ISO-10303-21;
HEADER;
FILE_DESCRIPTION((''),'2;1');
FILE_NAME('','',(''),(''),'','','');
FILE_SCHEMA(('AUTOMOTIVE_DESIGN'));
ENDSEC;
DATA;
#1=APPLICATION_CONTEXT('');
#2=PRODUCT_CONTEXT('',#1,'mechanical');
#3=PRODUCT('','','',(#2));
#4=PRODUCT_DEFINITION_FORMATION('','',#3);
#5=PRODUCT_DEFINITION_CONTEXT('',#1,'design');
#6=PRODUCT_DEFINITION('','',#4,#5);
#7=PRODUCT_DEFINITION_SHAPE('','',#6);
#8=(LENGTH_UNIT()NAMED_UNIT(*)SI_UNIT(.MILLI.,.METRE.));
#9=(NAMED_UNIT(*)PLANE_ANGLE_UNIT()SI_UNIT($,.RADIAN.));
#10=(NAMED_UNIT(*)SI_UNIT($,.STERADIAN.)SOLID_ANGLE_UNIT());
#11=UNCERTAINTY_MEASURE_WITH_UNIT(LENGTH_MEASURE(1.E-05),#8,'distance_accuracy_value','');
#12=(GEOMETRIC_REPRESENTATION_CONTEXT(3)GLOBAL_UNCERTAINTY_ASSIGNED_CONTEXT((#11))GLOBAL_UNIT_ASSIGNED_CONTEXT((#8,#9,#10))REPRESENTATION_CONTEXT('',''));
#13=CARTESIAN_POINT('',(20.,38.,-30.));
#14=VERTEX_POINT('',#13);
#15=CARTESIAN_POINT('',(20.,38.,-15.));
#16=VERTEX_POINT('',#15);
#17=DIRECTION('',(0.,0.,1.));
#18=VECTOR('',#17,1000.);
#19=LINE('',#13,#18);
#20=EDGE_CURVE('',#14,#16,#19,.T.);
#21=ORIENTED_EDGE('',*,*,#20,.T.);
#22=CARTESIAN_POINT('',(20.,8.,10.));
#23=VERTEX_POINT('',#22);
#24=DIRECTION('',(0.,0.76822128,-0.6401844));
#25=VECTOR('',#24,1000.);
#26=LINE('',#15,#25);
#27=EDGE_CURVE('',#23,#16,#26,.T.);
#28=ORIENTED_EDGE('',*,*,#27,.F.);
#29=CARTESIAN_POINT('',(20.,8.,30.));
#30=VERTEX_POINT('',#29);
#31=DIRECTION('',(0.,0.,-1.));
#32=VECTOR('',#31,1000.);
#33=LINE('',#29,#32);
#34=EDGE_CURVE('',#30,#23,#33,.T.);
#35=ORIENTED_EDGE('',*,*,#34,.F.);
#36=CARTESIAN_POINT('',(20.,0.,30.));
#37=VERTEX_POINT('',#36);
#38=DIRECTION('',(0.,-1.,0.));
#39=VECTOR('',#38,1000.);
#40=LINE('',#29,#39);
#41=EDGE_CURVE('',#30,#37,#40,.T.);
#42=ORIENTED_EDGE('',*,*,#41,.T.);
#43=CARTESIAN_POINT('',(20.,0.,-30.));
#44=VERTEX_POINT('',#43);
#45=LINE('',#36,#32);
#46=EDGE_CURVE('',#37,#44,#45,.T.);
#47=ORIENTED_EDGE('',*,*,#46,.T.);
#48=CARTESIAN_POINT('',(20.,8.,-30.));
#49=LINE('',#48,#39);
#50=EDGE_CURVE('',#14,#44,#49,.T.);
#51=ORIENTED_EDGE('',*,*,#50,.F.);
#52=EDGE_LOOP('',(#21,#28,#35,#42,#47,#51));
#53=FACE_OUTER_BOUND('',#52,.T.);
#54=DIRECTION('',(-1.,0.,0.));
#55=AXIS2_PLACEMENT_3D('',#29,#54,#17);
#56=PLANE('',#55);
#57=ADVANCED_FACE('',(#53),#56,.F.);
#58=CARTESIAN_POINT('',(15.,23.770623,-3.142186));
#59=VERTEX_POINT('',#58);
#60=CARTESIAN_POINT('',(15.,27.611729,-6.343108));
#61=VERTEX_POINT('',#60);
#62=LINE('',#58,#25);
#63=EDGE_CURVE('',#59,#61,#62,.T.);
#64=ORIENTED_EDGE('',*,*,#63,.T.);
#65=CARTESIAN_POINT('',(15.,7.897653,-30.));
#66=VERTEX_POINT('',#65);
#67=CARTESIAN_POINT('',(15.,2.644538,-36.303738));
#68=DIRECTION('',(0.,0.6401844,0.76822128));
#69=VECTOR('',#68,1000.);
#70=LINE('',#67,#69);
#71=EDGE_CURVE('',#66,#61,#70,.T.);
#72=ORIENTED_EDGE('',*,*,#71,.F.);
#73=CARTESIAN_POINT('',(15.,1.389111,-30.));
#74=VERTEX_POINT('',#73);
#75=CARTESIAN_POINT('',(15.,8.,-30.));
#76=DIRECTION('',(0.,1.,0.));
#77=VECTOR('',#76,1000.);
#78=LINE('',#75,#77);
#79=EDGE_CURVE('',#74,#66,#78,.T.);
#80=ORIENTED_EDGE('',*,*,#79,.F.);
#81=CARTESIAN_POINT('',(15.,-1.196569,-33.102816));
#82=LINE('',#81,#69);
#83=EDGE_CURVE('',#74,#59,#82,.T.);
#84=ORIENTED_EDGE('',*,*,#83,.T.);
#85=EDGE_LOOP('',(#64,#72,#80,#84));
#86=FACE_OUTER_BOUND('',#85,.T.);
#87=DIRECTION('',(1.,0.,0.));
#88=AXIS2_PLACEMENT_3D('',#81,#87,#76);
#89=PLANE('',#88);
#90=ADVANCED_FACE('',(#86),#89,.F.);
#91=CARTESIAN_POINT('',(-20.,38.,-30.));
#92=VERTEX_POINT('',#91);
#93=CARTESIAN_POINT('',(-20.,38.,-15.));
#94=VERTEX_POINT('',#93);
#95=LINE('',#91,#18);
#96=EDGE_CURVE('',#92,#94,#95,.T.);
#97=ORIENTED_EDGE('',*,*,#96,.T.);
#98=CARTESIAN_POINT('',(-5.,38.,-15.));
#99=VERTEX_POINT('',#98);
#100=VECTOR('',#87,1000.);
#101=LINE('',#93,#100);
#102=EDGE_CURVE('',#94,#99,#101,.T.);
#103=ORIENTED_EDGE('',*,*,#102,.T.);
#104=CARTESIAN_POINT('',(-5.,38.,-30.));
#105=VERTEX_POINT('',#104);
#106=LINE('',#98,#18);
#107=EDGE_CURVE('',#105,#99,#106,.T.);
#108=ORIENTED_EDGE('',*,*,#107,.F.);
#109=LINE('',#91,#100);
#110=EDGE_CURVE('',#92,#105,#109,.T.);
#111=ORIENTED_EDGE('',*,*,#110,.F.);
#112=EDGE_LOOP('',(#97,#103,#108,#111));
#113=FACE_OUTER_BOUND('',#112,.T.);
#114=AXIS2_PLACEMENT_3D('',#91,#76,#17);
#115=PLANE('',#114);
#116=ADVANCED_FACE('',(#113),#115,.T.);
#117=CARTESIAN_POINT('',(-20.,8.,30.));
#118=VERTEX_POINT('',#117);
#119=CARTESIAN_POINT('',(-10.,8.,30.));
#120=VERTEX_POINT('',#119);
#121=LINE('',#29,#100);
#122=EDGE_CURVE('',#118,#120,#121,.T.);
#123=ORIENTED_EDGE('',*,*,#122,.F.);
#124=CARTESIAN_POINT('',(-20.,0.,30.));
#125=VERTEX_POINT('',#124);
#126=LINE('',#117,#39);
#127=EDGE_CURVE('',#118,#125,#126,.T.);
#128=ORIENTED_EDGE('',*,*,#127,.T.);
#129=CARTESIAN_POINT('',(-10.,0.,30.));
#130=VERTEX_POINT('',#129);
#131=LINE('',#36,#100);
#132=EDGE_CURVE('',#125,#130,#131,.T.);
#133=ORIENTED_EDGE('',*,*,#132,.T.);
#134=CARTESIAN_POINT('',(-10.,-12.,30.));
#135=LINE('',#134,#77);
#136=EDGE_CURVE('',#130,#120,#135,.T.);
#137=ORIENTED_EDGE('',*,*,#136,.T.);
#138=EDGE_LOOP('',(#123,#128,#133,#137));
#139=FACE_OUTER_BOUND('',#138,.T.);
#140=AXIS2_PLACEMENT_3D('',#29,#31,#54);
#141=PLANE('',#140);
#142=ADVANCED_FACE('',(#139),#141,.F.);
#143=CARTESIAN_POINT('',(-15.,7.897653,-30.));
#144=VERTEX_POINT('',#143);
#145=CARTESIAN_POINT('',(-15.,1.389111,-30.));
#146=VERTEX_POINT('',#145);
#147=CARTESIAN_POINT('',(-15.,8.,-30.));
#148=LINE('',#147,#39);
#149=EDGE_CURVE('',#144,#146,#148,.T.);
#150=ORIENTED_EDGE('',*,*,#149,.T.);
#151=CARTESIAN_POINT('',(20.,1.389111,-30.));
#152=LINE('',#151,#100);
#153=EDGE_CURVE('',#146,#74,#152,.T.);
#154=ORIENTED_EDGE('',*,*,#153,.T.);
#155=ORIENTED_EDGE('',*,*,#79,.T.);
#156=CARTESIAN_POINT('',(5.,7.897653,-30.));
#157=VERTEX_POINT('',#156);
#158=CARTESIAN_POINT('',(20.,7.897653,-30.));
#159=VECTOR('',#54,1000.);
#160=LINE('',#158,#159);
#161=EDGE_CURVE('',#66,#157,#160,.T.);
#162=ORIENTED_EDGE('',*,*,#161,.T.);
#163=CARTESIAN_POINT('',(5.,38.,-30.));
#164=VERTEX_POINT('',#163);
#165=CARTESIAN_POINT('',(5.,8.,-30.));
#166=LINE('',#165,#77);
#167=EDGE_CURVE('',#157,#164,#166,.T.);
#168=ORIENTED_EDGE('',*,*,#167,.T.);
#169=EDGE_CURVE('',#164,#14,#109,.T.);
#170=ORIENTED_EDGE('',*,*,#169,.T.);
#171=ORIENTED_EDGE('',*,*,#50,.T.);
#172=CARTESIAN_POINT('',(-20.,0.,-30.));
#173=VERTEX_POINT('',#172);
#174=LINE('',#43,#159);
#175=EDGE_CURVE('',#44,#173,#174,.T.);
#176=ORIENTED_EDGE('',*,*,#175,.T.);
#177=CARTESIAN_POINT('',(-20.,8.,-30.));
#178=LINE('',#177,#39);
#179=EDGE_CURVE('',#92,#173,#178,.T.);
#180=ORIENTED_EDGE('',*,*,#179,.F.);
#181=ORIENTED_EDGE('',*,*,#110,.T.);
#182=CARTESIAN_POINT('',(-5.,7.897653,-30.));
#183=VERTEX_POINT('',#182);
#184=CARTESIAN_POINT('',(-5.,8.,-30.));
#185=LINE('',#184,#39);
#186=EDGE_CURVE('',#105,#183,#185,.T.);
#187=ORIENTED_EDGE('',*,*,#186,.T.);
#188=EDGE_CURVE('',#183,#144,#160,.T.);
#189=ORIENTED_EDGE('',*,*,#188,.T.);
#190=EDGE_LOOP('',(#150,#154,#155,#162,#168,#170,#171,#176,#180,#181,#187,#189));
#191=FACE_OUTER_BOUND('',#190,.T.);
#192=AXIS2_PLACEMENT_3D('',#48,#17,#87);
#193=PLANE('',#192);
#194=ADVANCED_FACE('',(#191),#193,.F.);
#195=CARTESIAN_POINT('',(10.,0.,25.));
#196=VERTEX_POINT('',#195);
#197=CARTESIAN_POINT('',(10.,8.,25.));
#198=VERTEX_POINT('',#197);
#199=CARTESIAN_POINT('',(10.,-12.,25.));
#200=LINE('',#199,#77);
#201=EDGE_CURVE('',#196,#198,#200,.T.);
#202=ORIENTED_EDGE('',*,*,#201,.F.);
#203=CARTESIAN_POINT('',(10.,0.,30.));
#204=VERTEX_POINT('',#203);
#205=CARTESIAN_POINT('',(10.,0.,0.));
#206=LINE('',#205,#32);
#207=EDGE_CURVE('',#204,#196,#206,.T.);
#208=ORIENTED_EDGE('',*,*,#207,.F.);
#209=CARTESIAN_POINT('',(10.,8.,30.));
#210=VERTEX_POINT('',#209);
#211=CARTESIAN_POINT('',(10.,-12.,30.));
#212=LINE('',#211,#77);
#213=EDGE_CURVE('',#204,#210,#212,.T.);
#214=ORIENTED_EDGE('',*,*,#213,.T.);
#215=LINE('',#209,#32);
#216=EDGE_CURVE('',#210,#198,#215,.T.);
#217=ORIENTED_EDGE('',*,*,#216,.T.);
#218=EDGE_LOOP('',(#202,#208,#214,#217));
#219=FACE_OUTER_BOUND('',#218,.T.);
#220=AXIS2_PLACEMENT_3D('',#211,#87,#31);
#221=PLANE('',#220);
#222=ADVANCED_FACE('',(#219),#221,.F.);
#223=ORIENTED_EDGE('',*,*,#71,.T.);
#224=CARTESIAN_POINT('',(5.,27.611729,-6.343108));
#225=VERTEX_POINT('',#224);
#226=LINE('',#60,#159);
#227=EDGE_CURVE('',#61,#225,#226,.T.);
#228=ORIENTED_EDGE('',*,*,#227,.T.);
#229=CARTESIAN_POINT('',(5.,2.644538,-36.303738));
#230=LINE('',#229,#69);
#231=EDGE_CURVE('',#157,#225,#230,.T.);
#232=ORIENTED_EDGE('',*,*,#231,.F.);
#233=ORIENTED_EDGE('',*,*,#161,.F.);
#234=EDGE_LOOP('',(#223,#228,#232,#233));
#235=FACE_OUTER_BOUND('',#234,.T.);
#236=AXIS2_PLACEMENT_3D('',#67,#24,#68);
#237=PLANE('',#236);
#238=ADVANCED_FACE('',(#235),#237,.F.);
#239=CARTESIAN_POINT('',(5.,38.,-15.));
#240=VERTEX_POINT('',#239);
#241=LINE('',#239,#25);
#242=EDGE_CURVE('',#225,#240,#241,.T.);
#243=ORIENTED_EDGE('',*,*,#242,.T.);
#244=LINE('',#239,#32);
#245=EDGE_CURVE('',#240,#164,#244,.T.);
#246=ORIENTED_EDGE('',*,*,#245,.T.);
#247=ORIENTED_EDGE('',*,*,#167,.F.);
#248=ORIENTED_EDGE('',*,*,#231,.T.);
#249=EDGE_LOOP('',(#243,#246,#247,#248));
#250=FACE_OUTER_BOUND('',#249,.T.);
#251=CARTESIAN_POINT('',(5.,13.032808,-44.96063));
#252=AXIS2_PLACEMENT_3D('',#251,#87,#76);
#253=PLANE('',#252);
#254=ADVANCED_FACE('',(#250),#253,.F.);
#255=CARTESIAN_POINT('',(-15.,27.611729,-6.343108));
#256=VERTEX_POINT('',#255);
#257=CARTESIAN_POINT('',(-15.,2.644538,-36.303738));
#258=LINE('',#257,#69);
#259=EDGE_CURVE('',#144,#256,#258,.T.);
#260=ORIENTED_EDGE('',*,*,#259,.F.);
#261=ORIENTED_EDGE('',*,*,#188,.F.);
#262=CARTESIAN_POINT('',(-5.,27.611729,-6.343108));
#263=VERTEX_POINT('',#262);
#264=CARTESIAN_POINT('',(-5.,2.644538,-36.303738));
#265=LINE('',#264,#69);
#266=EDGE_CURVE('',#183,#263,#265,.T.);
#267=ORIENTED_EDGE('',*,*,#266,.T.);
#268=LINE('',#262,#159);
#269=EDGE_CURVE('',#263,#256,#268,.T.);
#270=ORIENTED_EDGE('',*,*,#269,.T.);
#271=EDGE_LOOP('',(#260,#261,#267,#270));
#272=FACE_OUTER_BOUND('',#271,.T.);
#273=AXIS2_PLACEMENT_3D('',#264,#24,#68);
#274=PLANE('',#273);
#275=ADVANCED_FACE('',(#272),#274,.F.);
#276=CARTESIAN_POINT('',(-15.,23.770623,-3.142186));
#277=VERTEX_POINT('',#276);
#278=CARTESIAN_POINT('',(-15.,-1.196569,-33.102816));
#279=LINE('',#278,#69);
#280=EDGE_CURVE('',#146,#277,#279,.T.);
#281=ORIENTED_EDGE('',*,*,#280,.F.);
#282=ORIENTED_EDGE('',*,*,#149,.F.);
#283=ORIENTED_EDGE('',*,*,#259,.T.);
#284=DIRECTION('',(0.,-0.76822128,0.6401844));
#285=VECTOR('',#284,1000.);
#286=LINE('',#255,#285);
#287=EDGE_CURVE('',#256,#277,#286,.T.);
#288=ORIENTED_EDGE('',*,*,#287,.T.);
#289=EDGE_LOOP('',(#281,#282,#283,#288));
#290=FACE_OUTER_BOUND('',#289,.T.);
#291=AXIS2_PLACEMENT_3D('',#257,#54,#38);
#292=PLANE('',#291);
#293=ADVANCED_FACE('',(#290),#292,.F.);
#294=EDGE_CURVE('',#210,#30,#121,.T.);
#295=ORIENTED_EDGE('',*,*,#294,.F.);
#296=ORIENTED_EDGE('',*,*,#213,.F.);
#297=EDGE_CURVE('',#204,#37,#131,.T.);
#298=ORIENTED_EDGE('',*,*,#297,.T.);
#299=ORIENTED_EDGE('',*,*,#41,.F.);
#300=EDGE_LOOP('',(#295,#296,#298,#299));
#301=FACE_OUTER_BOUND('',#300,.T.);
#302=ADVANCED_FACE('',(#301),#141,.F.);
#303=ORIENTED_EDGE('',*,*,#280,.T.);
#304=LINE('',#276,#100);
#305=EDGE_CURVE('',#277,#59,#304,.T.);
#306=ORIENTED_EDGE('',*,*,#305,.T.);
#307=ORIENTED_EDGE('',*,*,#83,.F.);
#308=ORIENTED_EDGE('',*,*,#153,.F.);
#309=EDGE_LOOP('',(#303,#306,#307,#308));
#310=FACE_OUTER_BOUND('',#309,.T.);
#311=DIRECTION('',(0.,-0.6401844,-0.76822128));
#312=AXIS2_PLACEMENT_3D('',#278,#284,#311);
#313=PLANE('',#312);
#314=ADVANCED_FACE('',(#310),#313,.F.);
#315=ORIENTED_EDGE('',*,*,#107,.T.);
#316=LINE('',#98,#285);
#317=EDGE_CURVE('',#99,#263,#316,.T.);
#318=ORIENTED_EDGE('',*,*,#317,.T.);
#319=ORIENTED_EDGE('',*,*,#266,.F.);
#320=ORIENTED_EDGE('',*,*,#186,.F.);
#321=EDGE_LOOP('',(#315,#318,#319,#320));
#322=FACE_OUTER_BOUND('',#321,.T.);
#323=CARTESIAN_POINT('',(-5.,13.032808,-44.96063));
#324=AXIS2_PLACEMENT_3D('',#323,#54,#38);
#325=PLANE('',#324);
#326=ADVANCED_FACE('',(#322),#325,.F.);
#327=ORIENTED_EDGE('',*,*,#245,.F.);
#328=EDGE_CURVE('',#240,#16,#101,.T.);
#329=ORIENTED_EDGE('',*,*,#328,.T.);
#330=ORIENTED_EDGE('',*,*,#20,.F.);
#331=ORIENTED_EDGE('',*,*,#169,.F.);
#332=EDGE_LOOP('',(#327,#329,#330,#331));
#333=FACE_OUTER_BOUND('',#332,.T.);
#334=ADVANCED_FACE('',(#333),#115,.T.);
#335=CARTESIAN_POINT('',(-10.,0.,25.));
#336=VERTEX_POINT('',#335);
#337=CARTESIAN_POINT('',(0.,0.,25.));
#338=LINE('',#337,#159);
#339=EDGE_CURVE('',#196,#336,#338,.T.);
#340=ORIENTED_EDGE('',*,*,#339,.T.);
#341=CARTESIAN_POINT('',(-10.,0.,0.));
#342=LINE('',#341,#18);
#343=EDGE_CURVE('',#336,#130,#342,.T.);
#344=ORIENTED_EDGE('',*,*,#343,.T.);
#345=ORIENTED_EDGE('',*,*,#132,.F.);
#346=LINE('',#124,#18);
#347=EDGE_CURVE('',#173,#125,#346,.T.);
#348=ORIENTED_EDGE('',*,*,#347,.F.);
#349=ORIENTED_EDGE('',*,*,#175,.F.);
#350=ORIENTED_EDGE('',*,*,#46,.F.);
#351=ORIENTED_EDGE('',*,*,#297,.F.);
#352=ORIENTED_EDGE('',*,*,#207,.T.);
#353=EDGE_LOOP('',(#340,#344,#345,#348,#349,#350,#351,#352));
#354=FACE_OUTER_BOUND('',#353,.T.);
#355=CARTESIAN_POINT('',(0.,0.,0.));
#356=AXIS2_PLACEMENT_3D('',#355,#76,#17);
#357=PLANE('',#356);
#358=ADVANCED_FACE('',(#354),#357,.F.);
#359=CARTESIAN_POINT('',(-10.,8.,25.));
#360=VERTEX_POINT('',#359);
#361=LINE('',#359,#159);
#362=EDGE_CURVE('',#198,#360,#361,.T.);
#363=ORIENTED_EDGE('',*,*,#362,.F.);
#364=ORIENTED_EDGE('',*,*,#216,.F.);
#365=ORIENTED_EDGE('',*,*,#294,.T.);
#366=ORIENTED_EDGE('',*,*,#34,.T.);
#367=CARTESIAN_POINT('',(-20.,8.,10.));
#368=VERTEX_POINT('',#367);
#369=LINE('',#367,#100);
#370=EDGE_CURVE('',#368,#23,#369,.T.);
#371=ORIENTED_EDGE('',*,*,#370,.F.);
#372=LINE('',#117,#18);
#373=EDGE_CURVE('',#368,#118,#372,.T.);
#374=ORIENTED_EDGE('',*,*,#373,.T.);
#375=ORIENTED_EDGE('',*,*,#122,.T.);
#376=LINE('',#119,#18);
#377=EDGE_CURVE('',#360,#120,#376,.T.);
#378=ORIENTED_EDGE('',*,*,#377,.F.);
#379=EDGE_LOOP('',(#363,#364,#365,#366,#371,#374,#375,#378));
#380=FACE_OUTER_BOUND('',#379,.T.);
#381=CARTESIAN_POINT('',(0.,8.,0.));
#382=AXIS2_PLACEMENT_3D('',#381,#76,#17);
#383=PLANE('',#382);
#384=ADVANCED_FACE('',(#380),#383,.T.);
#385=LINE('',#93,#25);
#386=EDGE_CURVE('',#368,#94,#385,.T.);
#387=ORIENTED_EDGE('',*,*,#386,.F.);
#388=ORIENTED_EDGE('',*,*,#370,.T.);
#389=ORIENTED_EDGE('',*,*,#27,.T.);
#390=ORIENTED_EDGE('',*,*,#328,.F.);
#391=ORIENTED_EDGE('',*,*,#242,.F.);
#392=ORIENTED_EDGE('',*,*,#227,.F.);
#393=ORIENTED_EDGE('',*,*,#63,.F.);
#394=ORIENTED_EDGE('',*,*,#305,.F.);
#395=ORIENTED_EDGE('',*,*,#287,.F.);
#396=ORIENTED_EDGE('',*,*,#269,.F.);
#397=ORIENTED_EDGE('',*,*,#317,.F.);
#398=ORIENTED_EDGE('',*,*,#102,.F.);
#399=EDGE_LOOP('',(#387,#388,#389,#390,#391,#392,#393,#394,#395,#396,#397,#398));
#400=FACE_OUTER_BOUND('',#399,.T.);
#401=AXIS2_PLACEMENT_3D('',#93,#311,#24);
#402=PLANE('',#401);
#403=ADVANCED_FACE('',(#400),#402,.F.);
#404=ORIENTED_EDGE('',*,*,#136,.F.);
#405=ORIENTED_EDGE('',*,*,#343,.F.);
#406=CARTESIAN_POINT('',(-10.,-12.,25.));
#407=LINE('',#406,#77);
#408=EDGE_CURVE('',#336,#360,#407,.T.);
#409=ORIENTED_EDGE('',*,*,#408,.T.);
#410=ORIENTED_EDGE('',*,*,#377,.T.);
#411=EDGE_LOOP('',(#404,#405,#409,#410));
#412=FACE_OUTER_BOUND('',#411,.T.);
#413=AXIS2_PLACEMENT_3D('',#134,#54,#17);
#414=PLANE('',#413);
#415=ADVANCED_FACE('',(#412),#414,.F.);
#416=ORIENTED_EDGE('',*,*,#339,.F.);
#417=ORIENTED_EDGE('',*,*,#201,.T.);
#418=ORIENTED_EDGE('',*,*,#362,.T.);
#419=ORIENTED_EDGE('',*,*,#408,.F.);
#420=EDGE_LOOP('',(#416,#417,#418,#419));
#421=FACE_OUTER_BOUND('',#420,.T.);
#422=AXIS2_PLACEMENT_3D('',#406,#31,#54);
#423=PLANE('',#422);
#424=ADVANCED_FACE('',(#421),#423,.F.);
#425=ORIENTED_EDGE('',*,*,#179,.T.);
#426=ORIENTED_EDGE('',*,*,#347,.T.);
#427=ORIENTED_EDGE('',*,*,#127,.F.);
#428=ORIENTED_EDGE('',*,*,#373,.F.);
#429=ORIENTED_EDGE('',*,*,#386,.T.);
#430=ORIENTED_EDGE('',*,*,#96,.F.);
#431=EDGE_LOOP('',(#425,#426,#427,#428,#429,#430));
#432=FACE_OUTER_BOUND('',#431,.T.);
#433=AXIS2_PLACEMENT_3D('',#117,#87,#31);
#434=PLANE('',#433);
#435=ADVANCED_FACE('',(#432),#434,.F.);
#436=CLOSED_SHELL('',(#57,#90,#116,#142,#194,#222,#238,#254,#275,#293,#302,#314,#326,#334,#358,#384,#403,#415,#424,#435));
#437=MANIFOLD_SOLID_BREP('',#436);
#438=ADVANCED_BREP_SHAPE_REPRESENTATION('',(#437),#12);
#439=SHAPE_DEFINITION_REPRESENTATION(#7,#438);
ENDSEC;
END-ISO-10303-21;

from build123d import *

# Parameters (mm, degrees)
BASE_PLATE_SKETCH_W                   = 40
BASE_PLATE_SKETCH_H                   = 60
BASE_PLATE_60X40X8_DEPTH              = 8
BASE_NOTCH_SKETCH_W                   = 20
BASE_NOTCH_SKETCH_H                   = 5
BASE_NOTCH_20X5_DEPTH                 = 20
UPRIGHT_BLOCK_SKETCH_W                = 40
UPRIGHT_BLOCK_SKETCH_H                = 30
UPRIGHT_BLOCK_40X30X40_DEPTH          = 40
SLOPED_FACE_CUT_DEPTH                 = 40
TOP_SLOT_CUT_DEPTH                    = 39
ANGLED_SLOT_THROUGH_SLOPED_FACE_REACH = 54.383
ANGLED_SLOT_SKETCH_W                  = 10
ANGLED_SLOT_SKETCH_H                  = 15


with BuildPart() as part:
    # Base Plate Sketch → Base Plate 60x40x8 (new body)
    with BuildSketch(Plane(origin=(0, 0, 0), x_dir=(1, 0, 0), z_dir=(0, 1, 0))):
        Rectangle(BASE_PLATE_SKETCH_W, BASE_PLATE_SKETCH_H)
    extrude(amount=BASE_PLATE_60X40X8_DEPTH)

    # Base Notch Sketch → Base Notch 20x5 (cut)
    with BuildSketch(Plane(origin=(0, 8, 0), x_dir=(1, 0, 0), z_dir=(0, 1, 0))):
        with Locations((0, -27.5)):
            Rectangle(BASE_NOTCH_SKETCH_W, BASE_NOTCH_SKETCH_H)
    extrude(amount=-BASE_NOTCH_20X5_DEPTH, mode=Mode.SUBTRACT)

    # Upright Block Sketch → Upright Block 40x30x40 (add)
    with BuildSketch(Plane(origin=(20, 0, 0), x_dir=(0, 0, -1), z_dir=(1, 0, 0))):
        with Locations((10, 23)):
            Rectangle(UPRIGHT_BLOCK_SKETCH_W, UPRIGHT_BLOCK_SKETCH_H)
    extrude(amount=-UPRIGHT_BLOCK_40X30X40_DEPTH)

    # Slope Cut Sketch → Sloped Face Cut (cut)
    with BuildSketch(Plane(origin=(20, 0, 0), x_dir=(0, 0, -1), z_dir=(1, 0, 0))):
        Polygon((15, 38), (-10, 38), (-10, 8), align=None)
    extrude(amount=-SLOPED_FACE_CUT_DEPTH, mode=Mode.SUBTRACT)

    # Top Slot Sketch → Top Slot Cut (cut)
    with BuildSketch(Plane(origin=(0, 8.196721311, 9.836065574), x_dir=(1, 0, 0), z_dir=(0, 0.6401843996644799, 0.768221279597376))):
        Polygon((-5, 25.272676797), (-15, 25.272676797), (-15, 20.272676797), (15, 20.272676797), (15, 25.272676797), (5, 25.272676797), (5, 38.79517462), (-5, 38.79517462), align=None)
    extrude(amount=-TOP_SLOT_CUT_DEPTH, mode=Mode.SUBTRACT)

    # Angled Slot Sketch → Angled Slot Through Sloped Face (cut, up to next)
    with BuildSketch(Plane(origin=(0, 38, 0), x_dir=(1, 0, 0), z_dir=(0, 1, 0)), mode=Mode.PRIVATE) as angled_slot_through_sloped_face_sk1:
        with Locations((0, 22.5)):
            Rectangle(ANGLED_SLOT_SKETCH_W, ANGLED_SLOT_SKETCH_H)
    angled_slot_through_sloped_face_tool1 = extrude(angled_slot_through_sloped_face_sk1.sketch, amount=-ANGLED_SLOT_THROUGH_SLOPED_FACE_REACH, mode=Mode.PRIVATE) & part.part
    add(angled_slot_through_sloped_face_tool1.solids().sort_by_distance((0, 38, -22.5))[0], mode=Mode.SUBTRACT)


solid = part.part
